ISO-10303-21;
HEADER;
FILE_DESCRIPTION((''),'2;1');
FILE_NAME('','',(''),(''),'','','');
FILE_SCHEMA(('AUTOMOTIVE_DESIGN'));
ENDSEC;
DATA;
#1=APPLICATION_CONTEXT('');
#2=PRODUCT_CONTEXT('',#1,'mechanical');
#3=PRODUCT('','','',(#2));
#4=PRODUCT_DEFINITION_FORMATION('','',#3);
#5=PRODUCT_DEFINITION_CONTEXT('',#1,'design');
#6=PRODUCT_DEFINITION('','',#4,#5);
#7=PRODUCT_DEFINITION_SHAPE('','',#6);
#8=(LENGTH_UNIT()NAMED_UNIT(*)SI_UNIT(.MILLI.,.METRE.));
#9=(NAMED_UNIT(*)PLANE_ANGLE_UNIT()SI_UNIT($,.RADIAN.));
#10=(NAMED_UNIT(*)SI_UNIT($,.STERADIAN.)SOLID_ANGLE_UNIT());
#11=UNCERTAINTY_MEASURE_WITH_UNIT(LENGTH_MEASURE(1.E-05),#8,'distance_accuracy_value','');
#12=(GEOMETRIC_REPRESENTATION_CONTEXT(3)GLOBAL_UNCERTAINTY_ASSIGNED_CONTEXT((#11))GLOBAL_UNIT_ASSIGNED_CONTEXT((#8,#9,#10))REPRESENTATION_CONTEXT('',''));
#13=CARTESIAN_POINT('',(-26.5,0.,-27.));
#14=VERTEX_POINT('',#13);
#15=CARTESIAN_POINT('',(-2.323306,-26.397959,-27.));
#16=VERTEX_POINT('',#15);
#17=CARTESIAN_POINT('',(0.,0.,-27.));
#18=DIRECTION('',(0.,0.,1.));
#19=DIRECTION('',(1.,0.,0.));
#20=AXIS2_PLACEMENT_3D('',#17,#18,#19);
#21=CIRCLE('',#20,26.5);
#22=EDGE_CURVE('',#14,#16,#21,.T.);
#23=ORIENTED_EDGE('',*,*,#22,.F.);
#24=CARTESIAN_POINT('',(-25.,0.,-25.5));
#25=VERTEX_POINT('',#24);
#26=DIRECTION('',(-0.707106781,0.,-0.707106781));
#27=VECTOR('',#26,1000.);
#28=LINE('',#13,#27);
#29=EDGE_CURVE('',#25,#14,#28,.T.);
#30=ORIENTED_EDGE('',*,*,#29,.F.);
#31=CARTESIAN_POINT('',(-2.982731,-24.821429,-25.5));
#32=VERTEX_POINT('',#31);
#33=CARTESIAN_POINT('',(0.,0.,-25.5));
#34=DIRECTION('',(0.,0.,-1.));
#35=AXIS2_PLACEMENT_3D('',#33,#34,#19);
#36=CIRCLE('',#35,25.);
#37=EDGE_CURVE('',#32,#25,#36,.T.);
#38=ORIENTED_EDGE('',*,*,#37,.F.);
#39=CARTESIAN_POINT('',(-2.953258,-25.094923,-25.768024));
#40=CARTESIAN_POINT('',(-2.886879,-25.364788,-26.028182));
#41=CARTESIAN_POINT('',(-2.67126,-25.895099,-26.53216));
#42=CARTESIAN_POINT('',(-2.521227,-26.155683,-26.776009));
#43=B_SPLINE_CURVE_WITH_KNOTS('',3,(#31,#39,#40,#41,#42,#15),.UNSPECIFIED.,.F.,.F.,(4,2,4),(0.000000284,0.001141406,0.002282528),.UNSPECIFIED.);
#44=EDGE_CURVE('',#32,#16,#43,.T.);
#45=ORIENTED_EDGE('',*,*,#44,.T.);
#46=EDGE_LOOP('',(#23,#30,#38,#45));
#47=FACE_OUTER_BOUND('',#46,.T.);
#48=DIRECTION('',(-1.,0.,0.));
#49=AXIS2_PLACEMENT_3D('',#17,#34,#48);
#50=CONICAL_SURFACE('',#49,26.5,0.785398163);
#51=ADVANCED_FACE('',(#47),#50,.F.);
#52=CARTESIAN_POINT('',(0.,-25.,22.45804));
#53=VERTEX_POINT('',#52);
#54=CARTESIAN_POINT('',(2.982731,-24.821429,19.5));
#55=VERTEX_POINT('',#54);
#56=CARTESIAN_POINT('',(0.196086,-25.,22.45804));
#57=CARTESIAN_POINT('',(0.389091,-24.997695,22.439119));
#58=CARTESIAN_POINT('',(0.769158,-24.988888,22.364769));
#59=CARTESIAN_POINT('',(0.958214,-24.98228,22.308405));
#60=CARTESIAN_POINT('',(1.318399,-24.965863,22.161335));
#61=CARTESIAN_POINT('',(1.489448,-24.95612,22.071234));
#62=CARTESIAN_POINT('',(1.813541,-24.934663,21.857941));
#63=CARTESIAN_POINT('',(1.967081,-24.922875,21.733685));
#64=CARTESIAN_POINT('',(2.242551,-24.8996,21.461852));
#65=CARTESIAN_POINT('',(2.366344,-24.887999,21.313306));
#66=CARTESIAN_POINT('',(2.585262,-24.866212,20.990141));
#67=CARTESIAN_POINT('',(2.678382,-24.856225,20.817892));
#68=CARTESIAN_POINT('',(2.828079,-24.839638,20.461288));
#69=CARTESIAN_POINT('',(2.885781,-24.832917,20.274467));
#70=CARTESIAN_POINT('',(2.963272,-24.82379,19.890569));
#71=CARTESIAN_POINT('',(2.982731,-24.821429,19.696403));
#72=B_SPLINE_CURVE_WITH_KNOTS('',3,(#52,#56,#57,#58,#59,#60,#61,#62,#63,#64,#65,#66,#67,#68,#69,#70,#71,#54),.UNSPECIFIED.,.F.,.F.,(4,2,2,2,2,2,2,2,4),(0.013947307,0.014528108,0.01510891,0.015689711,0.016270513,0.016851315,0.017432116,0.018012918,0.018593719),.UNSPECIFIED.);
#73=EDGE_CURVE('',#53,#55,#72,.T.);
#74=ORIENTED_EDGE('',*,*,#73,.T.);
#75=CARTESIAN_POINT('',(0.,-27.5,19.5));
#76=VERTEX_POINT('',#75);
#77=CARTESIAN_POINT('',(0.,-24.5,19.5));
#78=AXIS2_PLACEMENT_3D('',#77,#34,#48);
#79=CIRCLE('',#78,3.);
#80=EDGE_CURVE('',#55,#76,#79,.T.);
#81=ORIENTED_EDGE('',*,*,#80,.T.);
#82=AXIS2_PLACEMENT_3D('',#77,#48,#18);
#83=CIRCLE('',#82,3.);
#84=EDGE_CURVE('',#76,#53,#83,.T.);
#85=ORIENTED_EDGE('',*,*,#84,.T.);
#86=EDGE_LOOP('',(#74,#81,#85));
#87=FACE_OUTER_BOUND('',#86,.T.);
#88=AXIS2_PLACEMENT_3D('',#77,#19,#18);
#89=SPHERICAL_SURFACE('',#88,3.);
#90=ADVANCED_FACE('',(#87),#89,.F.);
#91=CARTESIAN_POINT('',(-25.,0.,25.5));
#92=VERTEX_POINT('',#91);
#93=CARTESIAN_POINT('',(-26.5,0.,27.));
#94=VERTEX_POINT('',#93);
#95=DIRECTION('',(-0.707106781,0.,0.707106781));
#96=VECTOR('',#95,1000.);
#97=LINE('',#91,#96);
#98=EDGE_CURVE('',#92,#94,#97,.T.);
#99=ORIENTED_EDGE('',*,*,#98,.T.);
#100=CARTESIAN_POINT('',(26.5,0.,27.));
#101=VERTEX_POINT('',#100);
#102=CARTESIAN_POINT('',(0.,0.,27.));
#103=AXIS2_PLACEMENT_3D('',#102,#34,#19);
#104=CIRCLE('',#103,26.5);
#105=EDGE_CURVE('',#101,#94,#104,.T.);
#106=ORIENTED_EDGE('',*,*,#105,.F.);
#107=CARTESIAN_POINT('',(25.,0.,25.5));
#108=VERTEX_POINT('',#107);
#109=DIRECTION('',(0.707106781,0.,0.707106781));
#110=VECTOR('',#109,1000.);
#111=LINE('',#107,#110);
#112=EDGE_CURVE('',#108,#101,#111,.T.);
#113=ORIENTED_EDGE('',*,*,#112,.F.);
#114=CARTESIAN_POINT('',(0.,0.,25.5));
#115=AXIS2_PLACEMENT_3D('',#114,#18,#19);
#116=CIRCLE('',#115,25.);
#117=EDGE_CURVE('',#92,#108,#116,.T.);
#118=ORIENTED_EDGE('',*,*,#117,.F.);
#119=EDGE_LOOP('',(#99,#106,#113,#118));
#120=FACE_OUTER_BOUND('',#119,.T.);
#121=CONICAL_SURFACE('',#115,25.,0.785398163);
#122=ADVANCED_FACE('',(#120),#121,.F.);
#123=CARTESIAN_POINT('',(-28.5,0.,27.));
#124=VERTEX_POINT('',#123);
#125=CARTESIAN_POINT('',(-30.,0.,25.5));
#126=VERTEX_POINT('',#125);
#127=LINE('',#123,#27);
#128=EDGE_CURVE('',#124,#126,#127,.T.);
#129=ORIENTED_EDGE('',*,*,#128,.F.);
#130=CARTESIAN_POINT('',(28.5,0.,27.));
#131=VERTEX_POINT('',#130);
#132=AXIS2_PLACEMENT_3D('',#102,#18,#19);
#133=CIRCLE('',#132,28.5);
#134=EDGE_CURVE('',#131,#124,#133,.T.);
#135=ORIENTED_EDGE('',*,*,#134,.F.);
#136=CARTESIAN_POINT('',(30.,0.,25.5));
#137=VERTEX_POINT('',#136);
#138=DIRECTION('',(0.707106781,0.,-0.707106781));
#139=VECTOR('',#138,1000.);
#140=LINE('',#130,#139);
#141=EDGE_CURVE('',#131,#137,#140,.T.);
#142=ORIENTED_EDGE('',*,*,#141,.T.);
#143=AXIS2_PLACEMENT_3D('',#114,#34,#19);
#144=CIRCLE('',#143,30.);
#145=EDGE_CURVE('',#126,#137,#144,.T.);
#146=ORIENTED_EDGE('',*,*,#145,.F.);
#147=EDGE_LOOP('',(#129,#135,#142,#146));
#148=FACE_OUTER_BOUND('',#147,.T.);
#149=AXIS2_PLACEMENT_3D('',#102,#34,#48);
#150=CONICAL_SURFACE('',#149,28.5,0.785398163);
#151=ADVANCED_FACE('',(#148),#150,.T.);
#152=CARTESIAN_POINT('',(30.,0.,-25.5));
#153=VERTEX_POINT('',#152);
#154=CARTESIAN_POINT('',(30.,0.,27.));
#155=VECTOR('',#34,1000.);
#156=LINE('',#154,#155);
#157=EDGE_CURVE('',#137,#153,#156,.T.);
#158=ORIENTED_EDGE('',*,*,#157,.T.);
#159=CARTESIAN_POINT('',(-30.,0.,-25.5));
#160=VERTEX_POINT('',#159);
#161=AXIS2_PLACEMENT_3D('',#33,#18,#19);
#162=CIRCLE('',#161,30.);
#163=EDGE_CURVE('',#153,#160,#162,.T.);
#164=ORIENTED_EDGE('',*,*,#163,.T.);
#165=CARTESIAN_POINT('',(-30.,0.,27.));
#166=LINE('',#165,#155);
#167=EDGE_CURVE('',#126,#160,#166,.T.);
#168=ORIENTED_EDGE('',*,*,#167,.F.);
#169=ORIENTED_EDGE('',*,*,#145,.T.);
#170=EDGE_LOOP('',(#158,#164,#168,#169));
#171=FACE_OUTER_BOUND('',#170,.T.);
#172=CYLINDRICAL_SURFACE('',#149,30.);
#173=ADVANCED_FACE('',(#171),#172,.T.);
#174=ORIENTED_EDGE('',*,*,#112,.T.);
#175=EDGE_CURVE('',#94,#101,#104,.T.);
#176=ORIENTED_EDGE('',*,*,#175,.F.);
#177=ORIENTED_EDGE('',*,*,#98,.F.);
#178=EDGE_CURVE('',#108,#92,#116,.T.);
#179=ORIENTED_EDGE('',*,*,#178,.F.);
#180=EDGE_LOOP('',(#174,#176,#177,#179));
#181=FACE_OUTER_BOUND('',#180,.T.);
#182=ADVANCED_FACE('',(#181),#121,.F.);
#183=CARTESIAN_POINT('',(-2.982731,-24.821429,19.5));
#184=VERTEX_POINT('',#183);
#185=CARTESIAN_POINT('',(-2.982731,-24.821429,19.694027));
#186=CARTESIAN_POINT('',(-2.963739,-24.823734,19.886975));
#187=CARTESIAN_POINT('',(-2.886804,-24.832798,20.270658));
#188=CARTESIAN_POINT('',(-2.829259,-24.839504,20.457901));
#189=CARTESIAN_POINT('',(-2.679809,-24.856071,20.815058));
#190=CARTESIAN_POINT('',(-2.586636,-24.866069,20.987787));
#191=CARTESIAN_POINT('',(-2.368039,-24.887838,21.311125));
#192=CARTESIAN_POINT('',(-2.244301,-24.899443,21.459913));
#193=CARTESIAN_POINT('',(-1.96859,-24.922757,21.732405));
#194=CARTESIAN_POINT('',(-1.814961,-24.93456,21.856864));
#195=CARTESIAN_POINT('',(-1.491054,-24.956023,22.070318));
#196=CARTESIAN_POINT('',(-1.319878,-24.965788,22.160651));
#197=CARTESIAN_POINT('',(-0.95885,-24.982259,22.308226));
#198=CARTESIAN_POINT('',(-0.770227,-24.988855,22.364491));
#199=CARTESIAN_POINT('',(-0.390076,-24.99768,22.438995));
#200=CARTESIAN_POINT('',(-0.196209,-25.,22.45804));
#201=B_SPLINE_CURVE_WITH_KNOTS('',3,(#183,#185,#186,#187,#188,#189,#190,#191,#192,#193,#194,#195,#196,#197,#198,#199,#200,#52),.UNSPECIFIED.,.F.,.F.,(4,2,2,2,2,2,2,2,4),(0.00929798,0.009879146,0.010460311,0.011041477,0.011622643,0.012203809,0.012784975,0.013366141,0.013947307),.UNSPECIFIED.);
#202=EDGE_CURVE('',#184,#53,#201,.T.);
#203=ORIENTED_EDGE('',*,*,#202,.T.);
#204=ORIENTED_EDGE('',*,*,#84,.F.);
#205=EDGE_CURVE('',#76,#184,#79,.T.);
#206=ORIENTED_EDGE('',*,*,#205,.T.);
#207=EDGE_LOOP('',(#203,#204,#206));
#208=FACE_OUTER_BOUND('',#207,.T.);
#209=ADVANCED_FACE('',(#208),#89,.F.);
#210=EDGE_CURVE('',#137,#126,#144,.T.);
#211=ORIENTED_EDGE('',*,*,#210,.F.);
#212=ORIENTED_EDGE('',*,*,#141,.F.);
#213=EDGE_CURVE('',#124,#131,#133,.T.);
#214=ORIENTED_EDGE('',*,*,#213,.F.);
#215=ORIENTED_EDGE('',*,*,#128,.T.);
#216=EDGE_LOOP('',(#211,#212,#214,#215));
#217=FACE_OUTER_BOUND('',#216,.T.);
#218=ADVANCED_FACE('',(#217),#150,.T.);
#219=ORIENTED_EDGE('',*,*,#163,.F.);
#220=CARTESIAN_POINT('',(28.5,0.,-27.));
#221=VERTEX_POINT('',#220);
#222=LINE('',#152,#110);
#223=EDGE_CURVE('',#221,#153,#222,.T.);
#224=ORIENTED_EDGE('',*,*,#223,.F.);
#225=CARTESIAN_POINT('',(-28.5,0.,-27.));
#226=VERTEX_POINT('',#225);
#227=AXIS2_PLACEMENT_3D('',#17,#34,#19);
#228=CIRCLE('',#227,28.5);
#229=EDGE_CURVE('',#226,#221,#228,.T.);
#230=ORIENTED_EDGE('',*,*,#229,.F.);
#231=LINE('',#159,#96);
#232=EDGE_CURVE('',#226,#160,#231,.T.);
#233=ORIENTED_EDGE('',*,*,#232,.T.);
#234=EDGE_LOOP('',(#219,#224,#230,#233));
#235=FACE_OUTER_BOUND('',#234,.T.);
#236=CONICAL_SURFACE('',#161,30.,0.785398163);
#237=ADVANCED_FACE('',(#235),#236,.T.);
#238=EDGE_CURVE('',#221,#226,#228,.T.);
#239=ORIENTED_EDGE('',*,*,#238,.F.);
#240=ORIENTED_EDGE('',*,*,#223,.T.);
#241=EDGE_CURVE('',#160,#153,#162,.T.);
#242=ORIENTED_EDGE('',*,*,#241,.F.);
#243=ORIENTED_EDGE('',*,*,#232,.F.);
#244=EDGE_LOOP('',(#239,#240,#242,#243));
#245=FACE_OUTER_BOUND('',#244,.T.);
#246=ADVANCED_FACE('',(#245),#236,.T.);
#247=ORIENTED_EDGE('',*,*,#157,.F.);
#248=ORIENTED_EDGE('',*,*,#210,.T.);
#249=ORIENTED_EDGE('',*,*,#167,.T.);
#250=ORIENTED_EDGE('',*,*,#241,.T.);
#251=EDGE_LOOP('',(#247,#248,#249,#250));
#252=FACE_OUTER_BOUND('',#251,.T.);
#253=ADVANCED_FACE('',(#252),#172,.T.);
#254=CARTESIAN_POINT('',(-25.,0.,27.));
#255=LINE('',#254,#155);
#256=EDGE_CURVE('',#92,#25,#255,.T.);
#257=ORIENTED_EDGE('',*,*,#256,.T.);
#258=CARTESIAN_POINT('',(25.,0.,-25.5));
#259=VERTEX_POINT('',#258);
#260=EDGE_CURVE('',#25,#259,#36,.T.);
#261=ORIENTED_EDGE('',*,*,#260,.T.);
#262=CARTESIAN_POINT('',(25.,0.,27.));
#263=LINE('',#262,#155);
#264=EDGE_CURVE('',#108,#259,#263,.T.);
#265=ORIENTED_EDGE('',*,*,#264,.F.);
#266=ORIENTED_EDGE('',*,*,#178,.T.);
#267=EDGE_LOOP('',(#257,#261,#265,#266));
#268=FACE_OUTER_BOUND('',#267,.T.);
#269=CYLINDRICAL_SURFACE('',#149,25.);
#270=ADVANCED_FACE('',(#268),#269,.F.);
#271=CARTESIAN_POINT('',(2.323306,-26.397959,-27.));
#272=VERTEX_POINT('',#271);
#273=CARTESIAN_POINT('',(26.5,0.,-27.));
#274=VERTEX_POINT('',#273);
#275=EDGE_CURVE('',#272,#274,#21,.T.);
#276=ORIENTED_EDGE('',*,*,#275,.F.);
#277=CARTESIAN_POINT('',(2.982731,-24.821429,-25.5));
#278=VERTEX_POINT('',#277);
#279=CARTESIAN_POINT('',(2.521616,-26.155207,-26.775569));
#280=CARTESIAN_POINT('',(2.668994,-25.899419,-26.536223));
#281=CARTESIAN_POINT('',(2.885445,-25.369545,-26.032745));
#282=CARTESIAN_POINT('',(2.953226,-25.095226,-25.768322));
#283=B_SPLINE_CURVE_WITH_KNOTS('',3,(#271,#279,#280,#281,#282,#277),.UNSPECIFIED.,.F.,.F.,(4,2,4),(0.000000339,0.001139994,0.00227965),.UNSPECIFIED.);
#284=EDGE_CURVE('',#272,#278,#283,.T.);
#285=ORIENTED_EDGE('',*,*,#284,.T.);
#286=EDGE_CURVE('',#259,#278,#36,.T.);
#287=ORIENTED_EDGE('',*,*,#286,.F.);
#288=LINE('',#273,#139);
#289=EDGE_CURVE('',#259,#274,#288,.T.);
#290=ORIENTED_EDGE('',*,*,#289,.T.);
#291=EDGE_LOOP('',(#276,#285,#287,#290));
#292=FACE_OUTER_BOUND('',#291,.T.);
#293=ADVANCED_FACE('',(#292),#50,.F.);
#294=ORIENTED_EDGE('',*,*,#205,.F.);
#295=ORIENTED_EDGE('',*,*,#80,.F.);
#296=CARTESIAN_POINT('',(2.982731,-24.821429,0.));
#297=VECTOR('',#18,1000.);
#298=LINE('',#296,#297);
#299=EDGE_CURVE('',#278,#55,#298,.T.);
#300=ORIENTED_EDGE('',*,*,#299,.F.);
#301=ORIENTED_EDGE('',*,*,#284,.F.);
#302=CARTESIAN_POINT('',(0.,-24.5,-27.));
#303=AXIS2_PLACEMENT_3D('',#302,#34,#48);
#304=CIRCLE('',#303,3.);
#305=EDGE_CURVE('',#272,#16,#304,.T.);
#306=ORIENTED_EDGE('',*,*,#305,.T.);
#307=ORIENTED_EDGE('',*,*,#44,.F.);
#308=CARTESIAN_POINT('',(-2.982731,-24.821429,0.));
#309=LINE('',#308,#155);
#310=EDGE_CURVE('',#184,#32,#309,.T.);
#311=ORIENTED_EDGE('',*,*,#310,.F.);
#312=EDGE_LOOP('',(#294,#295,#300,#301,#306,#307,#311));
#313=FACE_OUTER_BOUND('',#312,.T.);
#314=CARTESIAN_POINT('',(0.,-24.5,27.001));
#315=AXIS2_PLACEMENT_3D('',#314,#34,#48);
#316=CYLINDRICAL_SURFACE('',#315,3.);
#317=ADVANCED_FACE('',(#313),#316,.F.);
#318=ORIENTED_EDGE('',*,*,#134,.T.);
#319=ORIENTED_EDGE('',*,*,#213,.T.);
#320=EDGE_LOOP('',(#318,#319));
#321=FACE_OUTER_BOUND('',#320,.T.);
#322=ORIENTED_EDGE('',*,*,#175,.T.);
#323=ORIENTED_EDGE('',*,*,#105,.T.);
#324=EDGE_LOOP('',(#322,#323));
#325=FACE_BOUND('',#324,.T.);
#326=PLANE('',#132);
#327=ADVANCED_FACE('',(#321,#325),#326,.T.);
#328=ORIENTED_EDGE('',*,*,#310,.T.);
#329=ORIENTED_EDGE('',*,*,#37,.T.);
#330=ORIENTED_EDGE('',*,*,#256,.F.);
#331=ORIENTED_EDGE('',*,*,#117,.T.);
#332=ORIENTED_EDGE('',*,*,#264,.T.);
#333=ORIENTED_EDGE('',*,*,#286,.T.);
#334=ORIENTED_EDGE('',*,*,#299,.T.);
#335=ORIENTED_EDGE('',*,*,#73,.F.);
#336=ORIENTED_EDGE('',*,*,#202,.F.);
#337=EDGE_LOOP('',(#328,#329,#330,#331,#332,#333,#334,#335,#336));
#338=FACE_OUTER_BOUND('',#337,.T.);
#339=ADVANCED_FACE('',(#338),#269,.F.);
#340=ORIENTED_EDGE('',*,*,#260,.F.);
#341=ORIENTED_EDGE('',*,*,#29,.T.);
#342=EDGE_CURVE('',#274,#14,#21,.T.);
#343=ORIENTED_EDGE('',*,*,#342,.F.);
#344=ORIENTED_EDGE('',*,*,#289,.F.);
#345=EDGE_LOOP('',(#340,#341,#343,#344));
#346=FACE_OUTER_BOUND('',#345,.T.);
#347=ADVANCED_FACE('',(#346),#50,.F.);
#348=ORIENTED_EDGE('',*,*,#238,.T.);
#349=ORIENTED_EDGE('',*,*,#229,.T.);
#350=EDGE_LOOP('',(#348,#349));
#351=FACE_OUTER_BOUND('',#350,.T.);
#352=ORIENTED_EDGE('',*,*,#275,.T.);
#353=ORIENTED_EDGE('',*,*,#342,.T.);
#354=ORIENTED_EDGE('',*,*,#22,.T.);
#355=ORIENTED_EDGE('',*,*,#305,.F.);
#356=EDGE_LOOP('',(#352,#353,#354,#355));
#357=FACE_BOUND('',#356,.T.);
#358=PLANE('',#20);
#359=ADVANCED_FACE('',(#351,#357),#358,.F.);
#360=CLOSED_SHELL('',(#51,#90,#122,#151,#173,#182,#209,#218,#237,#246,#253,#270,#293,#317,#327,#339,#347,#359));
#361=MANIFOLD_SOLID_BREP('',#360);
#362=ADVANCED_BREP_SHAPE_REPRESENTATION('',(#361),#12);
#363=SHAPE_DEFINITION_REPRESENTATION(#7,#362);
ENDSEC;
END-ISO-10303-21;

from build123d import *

# Parameters (mm, degrees)
SKETCH1_R           = 30
SKETCH1_R_2         = 25
BOSS_EXTRUDE1_DEPTH = 27
CHAMFER1_SIZE       = 1.5
CUT_EXTRUDE1_START  = -46.5
SKETCH2_R           = 3
CUT_EXTRUDE1_DEPTH  = 46.5


with BuildPart() as part:
    # Sketch1 → Boss-Extrude1 (new, symmetric)
    with BuildSketch(Plane.XY):
        Circle(SKETCH1_R)
        Circle(SKETCH1_R_2, mode=Mode.SUBTRACT)
    extrude(amount=BOSS_EXTRUDE1_DEPTH, both=True)

    # Chamfer1
    chamfer1_edges = [part.edges().sort_by_distance(p)[0] for p in [
        (-30, 0, -27),
        (-30, 0, 27),
        (-25, 0, -27),
        (-25, 0, 27),
    ]]
    chamfer(chamfer1_edges, length=CHAMFER1_SIZE)

    # Sketch3 → Cut-Revolve10 (revolve, cut)
    with BuildSketch(Plane(origin=(0, 0, 0), x_dir=(0, 0, -1), z_dir=(1, 0, 0))):
        with BuildLine():
            Line((-19.5, -21.5), (-19.5, -27.5))
            ThreePointArc((-19.5, -27.5), (-22.5, -24.5), (-19.5, -21.5))
        make_face()
    revolve(axis=Axis((0, -21.5, 19.5), (0, -1, 0)), mode=Mode.SUBTRACT)

    # Sketch2 → Cut-Extrude1 (cut)
    with BuildSketch(Plane(origin=(0, 0, -27), x_dir=(-1, 0, 0), z_dir=(0, 0, -1)).offset(CUT_EXTRUDE1_START)):
        with Locations((0, -24.5)):
            Circle(SKETCH2_R)
    extrude(amount=CUT_EXTRUDE1_DEPTH, mode=Mode.SUBTRACT)


solid = part.part
